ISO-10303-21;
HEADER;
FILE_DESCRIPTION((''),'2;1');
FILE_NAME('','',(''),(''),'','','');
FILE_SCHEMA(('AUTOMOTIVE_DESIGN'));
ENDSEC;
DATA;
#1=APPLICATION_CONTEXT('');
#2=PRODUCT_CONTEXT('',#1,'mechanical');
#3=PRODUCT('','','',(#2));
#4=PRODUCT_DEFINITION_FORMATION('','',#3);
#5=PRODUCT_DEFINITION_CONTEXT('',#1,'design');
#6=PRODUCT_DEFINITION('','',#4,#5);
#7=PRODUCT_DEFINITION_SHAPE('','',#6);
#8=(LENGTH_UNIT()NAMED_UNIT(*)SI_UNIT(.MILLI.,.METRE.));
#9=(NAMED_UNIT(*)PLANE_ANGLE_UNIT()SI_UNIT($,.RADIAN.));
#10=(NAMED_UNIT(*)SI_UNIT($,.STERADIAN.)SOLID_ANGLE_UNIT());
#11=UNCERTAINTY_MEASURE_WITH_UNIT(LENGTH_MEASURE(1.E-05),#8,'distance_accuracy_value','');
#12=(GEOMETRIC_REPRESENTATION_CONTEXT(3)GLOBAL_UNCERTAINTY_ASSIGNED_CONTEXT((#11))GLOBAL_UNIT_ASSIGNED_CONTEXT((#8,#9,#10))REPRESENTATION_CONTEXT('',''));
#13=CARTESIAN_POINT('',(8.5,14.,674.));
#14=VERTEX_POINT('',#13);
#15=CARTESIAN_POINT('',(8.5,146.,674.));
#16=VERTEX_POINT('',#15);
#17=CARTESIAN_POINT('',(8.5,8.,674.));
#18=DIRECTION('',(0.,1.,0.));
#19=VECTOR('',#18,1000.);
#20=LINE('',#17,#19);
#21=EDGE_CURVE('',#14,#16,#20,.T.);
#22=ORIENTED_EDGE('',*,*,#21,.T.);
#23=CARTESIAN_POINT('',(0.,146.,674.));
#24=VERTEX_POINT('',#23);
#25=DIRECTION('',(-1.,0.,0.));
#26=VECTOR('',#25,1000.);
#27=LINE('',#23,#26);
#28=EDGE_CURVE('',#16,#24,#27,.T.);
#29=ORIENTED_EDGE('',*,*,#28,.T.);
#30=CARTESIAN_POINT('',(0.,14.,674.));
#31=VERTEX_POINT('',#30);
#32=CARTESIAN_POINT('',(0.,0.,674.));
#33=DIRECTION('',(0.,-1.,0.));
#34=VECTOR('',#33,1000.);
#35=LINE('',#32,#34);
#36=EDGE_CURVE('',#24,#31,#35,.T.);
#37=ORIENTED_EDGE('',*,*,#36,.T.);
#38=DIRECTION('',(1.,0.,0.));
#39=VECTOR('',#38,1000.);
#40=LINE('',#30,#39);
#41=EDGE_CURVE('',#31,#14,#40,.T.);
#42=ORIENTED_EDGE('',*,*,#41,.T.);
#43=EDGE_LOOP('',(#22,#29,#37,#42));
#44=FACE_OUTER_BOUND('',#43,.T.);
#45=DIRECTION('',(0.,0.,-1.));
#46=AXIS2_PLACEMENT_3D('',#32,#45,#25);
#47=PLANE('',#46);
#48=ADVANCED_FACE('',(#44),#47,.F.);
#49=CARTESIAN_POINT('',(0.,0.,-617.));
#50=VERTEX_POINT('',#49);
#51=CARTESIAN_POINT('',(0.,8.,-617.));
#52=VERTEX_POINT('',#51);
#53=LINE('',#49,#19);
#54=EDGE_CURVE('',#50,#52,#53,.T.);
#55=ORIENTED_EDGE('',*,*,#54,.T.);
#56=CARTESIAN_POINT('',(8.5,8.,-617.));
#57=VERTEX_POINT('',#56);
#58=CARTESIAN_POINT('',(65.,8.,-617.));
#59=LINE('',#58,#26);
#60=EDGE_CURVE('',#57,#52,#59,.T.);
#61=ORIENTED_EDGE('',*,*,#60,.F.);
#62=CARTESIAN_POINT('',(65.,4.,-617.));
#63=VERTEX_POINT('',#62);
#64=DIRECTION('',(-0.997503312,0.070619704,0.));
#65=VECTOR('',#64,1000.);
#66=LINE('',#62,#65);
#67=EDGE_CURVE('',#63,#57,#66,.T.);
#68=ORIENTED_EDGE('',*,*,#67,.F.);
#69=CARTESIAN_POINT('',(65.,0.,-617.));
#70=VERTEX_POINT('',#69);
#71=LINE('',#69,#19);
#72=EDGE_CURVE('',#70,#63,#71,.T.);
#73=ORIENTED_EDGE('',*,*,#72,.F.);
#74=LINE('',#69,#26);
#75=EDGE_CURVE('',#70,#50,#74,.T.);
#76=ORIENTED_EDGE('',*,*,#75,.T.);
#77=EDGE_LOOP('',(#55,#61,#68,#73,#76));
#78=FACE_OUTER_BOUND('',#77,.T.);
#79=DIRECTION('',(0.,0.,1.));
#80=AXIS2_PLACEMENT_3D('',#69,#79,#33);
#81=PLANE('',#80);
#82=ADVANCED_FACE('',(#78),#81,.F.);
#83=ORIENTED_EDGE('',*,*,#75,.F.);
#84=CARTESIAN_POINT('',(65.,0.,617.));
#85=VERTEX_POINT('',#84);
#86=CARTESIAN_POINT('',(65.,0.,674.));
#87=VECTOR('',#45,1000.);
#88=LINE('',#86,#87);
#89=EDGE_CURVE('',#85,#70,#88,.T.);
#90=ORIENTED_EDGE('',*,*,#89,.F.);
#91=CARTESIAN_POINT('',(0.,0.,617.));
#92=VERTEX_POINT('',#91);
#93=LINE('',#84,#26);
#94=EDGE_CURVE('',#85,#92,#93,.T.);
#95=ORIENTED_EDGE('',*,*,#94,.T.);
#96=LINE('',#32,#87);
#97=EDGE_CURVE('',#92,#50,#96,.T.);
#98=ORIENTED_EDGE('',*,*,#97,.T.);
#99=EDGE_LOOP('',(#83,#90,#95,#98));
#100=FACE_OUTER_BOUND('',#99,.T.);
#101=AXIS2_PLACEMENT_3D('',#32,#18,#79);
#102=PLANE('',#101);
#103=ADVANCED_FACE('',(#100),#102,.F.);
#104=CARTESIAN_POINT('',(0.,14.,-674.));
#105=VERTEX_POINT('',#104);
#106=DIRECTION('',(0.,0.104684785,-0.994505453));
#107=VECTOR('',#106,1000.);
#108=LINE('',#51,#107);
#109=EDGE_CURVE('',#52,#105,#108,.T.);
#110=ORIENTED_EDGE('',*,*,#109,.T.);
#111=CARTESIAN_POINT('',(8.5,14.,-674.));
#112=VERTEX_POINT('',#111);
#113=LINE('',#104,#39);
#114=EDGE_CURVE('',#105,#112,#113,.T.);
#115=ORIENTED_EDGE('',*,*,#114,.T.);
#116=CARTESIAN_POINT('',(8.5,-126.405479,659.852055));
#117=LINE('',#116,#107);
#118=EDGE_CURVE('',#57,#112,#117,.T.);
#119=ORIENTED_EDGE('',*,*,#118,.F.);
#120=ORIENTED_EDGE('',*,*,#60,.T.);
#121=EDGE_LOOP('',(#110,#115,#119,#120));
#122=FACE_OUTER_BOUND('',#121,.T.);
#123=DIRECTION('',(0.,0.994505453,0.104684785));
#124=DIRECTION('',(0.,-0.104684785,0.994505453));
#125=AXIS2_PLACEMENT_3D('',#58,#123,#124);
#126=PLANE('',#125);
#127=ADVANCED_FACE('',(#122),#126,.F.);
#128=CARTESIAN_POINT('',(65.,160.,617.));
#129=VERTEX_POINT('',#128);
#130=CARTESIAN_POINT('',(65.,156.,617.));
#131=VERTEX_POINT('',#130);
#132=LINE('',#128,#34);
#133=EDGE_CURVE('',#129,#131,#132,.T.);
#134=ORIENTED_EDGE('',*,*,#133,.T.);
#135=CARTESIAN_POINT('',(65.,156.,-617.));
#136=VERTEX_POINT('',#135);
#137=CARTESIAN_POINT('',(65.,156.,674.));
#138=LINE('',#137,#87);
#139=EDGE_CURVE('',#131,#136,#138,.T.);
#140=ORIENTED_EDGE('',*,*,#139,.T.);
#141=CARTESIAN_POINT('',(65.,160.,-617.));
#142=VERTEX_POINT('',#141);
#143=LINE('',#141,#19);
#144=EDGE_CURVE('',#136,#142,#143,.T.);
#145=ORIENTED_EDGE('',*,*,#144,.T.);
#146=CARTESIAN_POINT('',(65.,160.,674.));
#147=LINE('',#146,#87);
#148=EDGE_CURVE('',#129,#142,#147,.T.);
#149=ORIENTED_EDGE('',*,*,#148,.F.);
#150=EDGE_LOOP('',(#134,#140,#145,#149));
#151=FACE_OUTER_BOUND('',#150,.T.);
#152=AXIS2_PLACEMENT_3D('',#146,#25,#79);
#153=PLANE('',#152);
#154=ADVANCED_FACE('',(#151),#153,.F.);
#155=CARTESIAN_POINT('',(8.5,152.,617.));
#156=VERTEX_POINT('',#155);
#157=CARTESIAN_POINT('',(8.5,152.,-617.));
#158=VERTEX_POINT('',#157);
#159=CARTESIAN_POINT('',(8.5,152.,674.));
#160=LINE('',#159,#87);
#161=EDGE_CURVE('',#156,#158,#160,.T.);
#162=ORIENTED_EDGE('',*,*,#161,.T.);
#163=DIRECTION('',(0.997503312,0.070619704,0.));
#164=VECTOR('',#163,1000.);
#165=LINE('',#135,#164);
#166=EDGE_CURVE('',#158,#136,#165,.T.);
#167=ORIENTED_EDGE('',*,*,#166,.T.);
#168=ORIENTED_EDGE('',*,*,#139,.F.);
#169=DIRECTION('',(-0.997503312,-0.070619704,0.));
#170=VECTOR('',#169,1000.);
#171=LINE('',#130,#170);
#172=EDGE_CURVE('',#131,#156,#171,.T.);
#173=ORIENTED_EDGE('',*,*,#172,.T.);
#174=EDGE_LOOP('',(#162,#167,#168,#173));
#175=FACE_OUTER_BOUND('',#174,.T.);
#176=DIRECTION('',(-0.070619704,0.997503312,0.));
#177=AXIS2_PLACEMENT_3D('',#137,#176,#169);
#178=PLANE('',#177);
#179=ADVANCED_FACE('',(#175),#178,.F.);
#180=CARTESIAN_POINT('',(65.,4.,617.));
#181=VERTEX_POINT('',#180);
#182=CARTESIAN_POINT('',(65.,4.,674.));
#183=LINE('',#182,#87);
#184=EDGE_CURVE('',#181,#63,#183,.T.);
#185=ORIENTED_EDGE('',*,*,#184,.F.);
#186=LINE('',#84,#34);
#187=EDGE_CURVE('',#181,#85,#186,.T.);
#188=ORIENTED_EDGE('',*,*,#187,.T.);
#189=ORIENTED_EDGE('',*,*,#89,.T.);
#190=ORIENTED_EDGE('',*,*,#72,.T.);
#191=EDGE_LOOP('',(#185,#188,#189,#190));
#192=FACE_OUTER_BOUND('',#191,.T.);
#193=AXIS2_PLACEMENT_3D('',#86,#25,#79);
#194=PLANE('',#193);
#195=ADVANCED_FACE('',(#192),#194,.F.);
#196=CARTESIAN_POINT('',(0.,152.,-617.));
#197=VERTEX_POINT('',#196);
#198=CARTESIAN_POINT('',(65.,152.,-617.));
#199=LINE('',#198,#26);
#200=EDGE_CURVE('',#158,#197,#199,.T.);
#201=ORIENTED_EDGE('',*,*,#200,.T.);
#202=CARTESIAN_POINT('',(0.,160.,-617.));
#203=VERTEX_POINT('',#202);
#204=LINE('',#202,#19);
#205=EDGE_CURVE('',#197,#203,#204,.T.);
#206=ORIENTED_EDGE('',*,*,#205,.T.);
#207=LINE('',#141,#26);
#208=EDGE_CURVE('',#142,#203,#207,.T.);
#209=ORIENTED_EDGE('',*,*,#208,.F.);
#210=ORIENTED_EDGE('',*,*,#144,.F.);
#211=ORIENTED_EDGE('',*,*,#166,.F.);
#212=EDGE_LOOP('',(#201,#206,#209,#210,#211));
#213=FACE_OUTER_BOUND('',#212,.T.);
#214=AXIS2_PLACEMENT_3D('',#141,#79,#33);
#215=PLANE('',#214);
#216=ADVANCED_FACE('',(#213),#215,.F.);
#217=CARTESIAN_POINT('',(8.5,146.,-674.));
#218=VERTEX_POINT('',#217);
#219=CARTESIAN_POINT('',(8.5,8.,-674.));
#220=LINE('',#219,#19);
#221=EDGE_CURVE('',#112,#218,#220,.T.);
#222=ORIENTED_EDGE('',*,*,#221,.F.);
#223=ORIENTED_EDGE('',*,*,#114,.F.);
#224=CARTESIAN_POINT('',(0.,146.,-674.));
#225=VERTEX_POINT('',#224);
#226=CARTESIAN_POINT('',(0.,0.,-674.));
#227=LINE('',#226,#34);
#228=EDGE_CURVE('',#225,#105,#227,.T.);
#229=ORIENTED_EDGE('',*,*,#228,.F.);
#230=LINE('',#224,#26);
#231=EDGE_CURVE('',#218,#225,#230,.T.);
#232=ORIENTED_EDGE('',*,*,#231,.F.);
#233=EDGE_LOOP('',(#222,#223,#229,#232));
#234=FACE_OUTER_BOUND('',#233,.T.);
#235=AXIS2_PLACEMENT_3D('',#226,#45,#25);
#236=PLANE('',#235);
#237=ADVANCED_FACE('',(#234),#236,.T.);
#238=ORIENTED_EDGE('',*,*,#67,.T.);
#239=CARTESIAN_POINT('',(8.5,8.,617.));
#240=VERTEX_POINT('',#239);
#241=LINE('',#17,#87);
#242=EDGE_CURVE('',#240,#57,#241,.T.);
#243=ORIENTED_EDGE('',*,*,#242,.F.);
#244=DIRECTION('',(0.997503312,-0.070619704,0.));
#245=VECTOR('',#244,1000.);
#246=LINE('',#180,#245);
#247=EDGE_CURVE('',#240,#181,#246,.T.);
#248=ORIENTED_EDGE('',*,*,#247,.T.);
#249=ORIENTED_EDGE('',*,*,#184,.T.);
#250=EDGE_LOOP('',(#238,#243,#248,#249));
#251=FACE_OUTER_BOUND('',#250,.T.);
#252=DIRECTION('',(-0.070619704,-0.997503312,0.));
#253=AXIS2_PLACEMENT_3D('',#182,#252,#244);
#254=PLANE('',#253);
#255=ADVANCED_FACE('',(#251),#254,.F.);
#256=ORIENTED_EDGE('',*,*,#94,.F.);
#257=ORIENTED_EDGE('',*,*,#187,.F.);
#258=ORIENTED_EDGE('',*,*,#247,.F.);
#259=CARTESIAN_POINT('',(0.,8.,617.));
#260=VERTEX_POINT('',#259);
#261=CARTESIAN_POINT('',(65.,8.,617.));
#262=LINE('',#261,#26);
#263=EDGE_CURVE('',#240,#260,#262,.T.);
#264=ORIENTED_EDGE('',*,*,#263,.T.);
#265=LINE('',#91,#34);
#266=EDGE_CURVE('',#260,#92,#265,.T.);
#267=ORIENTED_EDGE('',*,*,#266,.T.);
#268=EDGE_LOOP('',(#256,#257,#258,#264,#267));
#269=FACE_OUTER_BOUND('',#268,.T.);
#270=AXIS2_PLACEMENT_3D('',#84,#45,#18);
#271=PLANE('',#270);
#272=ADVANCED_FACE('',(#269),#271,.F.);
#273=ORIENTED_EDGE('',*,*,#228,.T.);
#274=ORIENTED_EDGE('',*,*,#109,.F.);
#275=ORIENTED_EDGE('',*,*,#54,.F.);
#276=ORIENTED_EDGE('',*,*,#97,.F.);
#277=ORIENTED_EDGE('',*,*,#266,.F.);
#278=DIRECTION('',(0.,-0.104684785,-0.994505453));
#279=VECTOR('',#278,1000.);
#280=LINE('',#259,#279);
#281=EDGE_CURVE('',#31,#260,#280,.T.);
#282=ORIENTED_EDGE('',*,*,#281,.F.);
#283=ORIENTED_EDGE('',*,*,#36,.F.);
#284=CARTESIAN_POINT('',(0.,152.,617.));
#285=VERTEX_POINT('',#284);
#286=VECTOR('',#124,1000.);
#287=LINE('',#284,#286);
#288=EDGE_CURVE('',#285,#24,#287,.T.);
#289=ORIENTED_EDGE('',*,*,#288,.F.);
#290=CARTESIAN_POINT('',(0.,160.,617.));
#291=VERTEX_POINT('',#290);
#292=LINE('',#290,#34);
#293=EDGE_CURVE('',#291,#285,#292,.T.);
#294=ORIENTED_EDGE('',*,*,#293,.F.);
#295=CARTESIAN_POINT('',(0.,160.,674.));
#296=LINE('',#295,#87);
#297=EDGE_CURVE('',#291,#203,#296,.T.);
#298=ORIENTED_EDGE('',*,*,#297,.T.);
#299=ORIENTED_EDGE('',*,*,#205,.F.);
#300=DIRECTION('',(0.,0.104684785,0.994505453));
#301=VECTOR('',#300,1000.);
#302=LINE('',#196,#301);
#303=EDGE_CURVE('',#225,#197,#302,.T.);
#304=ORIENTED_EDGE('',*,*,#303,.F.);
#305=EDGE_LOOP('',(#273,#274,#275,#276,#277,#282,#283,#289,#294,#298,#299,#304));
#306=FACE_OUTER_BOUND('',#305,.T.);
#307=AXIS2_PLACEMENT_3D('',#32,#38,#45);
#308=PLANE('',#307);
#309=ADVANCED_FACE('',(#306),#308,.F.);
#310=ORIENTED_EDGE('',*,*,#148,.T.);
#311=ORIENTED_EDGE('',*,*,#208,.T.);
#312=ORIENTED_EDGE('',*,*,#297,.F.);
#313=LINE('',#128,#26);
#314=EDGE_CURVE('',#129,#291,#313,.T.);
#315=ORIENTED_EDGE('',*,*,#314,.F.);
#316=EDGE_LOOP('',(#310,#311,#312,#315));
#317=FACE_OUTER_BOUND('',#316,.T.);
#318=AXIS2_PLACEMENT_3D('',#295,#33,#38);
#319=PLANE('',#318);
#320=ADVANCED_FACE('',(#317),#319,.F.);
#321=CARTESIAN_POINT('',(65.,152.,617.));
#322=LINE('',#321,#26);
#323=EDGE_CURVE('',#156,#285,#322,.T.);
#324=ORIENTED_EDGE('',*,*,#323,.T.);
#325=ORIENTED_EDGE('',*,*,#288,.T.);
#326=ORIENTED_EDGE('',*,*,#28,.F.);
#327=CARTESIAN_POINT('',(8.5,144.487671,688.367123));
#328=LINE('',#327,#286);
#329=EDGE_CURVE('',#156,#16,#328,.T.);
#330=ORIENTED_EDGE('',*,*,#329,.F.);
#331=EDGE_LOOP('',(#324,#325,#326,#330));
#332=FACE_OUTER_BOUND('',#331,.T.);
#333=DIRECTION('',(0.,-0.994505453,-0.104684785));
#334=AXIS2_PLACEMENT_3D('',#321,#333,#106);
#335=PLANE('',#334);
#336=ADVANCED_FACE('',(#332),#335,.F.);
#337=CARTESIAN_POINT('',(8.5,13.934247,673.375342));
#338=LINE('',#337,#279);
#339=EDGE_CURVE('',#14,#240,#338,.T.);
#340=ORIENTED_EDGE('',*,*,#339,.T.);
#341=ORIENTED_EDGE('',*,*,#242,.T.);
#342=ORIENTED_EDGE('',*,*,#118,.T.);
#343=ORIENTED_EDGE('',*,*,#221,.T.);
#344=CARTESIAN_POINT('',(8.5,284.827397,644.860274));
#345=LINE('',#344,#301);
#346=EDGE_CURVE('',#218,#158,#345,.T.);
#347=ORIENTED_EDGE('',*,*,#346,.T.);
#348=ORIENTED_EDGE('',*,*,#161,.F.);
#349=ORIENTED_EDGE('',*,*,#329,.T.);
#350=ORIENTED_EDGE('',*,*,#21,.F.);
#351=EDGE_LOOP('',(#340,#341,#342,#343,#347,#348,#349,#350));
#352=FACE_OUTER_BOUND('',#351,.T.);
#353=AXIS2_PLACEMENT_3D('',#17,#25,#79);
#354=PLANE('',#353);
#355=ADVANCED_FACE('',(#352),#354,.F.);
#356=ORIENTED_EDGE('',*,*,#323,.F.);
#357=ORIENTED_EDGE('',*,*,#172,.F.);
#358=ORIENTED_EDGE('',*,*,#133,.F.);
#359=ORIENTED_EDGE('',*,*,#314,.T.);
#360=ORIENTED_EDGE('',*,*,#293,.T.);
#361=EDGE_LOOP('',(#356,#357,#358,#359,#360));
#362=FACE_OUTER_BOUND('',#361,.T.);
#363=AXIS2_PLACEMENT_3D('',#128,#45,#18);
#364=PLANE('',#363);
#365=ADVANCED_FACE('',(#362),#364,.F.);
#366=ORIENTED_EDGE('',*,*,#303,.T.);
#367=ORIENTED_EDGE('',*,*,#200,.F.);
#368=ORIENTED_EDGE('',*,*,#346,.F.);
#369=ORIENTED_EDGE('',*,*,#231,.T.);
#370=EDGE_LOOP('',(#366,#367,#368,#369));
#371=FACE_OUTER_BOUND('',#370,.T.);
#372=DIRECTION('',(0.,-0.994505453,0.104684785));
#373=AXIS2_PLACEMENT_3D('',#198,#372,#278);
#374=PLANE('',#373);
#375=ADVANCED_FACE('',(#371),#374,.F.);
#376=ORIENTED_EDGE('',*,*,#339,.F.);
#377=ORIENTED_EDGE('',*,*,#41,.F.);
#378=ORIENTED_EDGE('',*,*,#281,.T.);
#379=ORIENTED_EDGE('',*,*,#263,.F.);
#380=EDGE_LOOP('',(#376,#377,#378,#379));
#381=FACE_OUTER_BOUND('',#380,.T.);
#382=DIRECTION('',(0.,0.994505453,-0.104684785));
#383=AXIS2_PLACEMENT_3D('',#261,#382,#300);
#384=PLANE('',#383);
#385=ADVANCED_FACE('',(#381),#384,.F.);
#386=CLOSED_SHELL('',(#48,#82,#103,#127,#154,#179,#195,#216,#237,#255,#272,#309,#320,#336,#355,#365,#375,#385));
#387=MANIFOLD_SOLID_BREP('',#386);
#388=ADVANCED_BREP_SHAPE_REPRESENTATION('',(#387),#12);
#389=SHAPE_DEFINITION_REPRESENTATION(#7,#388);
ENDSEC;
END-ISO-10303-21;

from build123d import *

# Parameters (mm, degrees)
EXTRUDE_1_DEPTH     = 674
CUT_EXTRUDE_1_DEPTH = 696.773670097


with BuildPart() as part:
    # 草图1 → 凸台-拉伸1 (new, symmetric)
    with BuildSketch(Plane.XY):
        Polygon((0, 0), (65, 0), (65, 4), (8.5, 8), (8.5, 152), (65, 156), (65, 160), (0, 160), align=None)
    extrude(amount=EXTRUDE_1_DEPTH, both=True)

    # 草图4 → 切除-拉伸1 (cut, through all)
    with BuildSketch(Plane.ZY):
        Polygon((-674, 160), (-617, 160), (-617, 152), (-674, 146), align=None)
        Polygon((674, 146), (674, 160), (617, 160), (617, 152), align=None)
        Polygon((674, 0), (617, 0), (617, 8), (674, 14), align=None)
        Polygon((-674, 14), (-674, 0), (-617, 0), (-617, 8), align=None)
    extrude(amount=-CUT_EXTRUDE_1_DEPTH, mode=Mode.SUBTRACT)


solid = part.part
